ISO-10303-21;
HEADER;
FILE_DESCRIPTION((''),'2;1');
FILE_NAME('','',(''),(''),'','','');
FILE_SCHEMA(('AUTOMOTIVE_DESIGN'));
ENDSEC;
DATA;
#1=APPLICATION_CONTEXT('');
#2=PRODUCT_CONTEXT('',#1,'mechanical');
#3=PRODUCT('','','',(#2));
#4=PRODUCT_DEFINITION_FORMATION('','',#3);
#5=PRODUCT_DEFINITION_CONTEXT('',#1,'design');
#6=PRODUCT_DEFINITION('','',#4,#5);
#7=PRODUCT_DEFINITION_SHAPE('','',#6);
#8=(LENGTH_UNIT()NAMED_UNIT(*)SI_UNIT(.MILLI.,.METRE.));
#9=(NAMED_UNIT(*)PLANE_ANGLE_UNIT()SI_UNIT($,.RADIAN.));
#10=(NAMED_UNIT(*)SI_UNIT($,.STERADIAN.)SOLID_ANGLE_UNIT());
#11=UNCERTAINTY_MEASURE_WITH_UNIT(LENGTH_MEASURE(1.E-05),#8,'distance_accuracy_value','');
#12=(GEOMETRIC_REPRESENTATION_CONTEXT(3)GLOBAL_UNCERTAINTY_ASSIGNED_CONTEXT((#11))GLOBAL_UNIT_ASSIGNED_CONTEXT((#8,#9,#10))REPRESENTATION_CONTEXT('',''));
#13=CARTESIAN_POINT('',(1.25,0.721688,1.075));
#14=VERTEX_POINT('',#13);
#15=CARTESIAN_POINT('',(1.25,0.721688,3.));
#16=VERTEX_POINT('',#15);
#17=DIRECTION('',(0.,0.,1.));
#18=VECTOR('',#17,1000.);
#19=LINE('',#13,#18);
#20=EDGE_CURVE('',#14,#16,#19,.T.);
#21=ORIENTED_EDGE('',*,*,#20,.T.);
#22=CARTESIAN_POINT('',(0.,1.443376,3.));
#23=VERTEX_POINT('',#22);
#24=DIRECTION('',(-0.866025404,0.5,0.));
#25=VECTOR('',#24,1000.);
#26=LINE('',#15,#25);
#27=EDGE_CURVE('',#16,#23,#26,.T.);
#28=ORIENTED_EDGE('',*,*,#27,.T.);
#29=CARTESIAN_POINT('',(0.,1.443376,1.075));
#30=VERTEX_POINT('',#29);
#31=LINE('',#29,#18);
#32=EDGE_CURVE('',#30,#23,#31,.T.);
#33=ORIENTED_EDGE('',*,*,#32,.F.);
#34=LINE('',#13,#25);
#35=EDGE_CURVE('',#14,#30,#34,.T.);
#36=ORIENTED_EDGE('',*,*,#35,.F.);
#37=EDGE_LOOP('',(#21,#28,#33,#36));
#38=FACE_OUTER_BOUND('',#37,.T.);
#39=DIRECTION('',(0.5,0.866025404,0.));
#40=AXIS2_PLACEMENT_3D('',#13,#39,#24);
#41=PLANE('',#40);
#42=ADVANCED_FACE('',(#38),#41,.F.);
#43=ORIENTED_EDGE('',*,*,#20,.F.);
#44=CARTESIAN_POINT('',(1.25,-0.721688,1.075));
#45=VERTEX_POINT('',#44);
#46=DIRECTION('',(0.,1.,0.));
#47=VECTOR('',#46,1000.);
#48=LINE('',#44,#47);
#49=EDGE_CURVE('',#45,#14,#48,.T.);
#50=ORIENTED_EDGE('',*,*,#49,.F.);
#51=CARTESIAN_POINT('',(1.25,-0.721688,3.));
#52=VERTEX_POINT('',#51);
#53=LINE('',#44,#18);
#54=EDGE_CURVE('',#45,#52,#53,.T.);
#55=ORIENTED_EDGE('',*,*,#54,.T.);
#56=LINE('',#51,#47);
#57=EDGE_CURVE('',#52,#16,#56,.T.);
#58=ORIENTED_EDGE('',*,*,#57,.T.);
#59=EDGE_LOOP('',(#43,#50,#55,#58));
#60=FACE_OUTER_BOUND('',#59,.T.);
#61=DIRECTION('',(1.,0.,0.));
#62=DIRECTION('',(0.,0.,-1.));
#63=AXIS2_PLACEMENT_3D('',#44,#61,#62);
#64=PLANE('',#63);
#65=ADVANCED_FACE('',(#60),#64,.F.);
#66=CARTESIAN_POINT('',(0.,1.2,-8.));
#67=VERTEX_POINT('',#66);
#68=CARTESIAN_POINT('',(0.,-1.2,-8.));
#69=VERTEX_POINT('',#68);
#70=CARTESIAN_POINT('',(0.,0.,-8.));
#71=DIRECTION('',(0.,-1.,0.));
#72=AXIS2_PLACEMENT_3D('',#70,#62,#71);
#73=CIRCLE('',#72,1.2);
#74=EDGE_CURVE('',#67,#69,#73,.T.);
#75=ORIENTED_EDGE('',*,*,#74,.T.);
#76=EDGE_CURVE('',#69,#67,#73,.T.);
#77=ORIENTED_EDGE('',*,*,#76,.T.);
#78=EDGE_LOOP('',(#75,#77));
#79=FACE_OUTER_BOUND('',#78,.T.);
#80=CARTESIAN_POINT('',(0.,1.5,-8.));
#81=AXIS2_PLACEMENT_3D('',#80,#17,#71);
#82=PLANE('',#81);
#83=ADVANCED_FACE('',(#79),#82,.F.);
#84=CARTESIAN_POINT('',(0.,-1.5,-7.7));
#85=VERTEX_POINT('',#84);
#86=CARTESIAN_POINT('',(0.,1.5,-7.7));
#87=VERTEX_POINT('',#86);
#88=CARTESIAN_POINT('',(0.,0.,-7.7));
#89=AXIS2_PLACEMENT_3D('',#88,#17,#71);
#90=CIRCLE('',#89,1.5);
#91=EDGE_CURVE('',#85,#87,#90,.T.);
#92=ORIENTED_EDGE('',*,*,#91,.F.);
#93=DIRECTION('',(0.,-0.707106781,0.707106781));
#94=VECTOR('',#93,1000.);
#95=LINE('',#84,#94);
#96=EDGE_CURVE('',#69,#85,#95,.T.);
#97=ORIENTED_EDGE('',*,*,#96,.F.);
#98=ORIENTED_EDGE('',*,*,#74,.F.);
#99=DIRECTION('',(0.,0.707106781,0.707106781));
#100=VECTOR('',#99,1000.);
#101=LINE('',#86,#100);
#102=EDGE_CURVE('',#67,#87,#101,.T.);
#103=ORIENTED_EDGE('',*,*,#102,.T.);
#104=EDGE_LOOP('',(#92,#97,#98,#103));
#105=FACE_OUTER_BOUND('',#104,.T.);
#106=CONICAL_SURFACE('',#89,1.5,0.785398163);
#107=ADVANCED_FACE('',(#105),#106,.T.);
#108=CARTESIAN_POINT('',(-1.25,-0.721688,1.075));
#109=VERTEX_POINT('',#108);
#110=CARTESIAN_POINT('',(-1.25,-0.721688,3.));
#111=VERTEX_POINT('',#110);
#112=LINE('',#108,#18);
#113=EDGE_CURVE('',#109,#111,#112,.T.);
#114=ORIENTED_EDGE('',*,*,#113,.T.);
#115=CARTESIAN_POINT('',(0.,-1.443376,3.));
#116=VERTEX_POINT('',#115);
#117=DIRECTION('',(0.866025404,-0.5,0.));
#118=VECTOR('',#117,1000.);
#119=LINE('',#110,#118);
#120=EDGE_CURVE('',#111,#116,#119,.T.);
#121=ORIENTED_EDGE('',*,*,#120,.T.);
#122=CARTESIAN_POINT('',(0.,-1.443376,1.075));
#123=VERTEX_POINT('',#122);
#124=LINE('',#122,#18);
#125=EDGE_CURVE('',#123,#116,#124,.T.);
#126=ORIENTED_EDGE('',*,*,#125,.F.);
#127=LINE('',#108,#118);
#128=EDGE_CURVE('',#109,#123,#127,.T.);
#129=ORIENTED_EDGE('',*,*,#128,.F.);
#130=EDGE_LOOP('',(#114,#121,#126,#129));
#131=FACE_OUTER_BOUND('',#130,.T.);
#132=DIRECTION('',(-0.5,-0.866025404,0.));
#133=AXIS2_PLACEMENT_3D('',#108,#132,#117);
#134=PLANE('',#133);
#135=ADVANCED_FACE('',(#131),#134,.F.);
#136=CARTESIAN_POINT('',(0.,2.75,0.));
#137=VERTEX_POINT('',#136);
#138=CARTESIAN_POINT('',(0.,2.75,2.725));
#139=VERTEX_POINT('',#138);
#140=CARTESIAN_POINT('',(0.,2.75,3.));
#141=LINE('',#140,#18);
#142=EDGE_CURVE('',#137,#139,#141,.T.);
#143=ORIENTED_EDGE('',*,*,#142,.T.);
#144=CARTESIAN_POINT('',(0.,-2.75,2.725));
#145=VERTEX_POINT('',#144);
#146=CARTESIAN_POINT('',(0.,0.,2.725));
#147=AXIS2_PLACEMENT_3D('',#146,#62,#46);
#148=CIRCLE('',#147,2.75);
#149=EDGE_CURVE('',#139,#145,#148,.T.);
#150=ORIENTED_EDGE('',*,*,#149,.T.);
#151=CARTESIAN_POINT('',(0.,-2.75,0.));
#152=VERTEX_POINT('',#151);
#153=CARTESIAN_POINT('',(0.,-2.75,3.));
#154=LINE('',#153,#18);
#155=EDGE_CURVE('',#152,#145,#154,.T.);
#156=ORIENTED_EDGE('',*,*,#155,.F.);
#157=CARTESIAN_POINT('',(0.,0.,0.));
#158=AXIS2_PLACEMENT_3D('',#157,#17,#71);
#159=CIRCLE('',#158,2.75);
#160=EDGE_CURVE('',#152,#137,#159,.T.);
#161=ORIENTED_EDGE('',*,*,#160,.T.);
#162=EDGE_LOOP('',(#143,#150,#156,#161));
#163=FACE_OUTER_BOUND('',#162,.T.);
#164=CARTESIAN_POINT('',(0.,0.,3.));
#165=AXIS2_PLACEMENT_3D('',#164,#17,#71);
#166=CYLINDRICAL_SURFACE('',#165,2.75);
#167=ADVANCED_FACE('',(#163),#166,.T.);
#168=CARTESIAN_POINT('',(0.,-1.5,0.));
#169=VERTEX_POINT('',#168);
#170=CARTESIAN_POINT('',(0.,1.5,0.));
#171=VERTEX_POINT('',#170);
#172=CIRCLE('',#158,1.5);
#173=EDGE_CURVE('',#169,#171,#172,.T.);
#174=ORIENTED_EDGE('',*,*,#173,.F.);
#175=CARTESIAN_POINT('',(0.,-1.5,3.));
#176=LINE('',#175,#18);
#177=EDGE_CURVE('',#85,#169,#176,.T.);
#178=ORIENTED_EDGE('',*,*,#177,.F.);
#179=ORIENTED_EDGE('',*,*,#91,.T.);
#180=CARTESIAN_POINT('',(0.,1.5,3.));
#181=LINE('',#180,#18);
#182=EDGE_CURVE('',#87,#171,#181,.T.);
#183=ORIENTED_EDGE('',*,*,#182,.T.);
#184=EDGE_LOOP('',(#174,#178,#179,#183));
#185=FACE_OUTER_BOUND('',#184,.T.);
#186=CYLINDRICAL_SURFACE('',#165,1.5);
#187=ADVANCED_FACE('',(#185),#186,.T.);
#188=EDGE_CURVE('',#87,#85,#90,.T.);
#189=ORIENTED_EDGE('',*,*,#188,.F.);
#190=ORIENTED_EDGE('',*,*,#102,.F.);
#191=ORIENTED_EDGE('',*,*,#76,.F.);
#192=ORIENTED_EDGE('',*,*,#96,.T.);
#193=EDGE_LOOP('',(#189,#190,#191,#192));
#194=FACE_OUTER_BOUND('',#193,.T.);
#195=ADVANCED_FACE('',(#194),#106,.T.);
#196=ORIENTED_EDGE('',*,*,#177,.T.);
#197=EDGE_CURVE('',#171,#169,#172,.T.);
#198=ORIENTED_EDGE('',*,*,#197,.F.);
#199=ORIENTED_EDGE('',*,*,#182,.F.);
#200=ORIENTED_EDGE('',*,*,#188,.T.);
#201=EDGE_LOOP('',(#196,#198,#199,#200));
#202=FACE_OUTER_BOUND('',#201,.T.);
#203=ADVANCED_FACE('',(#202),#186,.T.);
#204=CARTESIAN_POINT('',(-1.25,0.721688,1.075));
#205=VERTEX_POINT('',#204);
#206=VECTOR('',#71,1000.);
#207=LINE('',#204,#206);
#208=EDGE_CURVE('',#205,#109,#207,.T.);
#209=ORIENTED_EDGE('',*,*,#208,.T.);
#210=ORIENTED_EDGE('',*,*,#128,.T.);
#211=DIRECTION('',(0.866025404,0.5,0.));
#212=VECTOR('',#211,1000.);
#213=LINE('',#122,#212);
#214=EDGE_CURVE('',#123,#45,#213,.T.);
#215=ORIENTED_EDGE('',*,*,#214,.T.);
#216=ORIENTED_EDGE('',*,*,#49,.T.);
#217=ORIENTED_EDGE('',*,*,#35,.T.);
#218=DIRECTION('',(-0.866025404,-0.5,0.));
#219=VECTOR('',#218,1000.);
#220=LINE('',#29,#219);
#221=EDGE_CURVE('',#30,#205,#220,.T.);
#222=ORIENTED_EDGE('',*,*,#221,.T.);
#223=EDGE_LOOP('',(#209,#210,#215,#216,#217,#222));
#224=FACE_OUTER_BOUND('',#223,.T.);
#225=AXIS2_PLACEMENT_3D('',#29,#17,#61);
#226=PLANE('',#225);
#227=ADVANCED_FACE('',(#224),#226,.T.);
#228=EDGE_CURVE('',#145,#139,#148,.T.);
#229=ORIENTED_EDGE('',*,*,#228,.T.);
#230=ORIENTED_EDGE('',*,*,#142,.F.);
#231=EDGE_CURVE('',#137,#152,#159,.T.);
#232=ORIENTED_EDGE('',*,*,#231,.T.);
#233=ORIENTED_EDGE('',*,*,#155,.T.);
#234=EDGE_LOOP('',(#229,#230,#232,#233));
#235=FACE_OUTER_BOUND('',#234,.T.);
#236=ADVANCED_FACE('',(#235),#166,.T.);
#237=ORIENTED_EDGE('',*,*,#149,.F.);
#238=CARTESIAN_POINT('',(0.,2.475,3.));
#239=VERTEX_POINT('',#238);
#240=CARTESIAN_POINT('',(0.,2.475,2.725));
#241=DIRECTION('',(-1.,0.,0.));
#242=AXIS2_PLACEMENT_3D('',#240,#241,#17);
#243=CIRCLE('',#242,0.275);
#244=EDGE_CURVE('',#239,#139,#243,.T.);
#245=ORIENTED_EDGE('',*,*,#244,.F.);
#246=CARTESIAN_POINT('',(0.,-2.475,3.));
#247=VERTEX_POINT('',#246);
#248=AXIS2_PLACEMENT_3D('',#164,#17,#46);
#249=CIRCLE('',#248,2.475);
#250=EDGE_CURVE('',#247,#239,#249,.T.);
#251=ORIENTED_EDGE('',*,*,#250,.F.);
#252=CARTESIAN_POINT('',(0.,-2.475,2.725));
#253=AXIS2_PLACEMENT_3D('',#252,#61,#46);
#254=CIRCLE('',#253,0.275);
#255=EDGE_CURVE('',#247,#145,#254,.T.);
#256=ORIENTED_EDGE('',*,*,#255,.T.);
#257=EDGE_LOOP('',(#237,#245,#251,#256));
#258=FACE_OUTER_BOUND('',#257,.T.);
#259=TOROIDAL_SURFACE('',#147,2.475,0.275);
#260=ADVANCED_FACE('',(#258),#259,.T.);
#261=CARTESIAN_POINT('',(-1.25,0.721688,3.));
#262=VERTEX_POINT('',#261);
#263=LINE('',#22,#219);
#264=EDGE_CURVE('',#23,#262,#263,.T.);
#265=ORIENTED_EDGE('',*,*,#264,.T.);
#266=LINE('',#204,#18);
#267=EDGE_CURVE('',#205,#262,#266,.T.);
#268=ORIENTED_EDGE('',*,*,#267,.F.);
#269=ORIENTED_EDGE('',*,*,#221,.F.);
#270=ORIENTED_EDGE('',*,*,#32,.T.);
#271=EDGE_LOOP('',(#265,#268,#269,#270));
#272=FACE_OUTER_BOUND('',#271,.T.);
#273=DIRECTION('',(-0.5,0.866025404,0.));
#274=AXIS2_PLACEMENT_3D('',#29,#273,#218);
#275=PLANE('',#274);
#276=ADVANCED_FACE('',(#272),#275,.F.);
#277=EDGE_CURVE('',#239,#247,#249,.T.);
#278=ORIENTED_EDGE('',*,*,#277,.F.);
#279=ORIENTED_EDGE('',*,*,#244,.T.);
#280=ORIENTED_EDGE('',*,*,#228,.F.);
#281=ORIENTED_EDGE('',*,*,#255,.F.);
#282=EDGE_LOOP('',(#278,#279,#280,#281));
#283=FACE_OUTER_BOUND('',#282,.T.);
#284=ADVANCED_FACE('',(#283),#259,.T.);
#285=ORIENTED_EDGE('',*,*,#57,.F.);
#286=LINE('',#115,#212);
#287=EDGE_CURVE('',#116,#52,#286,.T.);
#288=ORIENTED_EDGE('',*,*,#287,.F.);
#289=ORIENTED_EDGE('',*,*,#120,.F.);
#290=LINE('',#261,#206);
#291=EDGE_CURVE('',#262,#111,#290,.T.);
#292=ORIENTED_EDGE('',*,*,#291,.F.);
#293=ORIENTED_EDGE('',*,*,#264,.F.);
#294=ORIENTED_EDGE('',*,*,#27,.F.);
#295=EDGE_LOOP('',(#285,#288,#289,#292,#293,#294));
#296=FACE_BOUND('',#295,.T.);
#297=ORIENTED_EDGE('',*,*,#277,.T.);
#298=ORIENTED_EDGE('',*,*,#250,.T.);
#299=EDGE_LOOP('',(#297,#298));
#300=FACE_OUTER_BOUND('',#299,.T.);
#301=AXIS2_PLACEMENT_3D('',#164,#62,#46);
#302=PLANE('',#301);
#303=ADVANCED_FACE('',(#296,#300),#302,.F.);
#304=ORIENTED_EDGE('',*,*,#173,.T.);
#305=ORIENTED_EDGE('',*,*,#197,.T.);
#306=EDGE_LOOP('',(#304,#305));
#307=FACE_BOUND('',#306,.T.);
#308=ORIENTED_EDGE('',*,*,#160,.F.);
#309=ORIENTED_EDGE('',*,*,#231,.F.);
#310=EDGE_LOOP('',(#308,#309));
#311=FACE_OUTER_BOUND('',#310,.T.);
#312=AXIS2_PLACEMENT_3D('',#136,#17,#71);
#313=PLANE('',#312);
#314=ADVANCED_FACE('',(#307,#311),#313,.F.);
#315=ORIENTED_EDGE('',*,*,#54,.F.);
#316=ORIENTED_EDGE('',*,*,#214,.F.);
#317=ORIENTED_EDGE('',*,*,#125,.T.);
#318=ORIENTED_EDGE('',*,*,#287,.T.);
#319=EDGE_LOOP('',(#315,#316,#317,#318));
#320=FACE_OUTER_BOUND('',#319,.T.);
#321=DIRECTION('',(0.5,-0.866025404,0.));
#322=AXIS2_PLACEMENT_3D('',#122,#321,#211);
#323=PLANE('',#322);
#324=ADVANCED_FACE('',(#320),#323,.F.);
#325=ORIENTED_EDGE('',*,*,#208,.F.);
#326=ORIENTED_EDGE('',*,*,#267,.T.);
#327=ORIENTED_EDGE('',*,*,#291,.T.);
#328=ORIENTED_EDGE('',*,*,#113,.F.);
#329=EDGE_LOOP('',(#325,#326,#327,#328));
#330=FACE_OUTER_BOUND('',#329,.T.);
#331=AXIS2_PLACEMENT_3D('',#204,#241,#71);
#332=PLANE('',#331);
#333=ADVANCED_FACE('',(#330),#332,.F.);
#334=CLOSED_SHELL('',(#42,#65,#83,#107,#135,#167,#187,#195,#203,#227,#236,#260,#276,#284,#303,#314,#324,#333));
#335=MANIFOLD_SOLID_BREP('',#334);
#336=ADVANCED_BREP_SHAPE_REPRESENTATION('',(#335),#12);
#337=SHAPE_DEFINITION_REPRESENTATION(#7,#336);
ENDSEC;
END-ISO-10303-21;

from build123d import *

# Parameters (mm, degrees)
CUT_EXTRUDE_1_DEPTH = 1.925
FILLET_1_R          = 0.275
CHAMFER_1_SIZE      = 0.3


with BuildPart() as part:
    # 草图3 → 旋转1 (revolve)
    with BuildSketch(Plane(origin=(0, 0, 0), x_dir=(0, 0, -1), z_dir=(1, 0, 0)), mode=Mode.PRIVATE) as revolve_1_sk:
        Polygon((-3, 0), (-3, 2.75), (0, 2.75), (0, 1.5), (8, 1.5), (8, 0), align=None)
    revolve(revolve_1_sk.sketch.rotate(Axis((0, 0, 3), (0, 0, -1)), 180), axis=Axis((0, 0, 3), (0, 0, -1)))

    # 草图4 → 切除-拉伸1 (cut)
    with BuildSketch(Plane.XY.offset(3)):
        Polygon((0, 1.443375673), (-1.25, 0.721687836), (-1.25, -0.721687836), (0, -1.443375673), (1.25, -0.721687836), (1.25, 0.721687836), align=None)
    extrude(amount=-CUT_EXTRUDE_1_DEPTH, mode=Mode.SUBTRACT)

    # 圆角1
    fillet_1_edges = [part.edges().sort_by_distance(p)[0] for p in [
        (0, 2.75, 3),
    ]]
    fillet(fillet_1_edges, radius=FILLET_1_R)

    # 倒角1
    chamfer_1_edges = [part.edges().sort_by_distance(p)[0] for p in [
        (0, 1.5, -8),
    ]]
    chamfer(chamfer_1_edges, length=CHAMFER_1_SIZE)


solid = part.part
